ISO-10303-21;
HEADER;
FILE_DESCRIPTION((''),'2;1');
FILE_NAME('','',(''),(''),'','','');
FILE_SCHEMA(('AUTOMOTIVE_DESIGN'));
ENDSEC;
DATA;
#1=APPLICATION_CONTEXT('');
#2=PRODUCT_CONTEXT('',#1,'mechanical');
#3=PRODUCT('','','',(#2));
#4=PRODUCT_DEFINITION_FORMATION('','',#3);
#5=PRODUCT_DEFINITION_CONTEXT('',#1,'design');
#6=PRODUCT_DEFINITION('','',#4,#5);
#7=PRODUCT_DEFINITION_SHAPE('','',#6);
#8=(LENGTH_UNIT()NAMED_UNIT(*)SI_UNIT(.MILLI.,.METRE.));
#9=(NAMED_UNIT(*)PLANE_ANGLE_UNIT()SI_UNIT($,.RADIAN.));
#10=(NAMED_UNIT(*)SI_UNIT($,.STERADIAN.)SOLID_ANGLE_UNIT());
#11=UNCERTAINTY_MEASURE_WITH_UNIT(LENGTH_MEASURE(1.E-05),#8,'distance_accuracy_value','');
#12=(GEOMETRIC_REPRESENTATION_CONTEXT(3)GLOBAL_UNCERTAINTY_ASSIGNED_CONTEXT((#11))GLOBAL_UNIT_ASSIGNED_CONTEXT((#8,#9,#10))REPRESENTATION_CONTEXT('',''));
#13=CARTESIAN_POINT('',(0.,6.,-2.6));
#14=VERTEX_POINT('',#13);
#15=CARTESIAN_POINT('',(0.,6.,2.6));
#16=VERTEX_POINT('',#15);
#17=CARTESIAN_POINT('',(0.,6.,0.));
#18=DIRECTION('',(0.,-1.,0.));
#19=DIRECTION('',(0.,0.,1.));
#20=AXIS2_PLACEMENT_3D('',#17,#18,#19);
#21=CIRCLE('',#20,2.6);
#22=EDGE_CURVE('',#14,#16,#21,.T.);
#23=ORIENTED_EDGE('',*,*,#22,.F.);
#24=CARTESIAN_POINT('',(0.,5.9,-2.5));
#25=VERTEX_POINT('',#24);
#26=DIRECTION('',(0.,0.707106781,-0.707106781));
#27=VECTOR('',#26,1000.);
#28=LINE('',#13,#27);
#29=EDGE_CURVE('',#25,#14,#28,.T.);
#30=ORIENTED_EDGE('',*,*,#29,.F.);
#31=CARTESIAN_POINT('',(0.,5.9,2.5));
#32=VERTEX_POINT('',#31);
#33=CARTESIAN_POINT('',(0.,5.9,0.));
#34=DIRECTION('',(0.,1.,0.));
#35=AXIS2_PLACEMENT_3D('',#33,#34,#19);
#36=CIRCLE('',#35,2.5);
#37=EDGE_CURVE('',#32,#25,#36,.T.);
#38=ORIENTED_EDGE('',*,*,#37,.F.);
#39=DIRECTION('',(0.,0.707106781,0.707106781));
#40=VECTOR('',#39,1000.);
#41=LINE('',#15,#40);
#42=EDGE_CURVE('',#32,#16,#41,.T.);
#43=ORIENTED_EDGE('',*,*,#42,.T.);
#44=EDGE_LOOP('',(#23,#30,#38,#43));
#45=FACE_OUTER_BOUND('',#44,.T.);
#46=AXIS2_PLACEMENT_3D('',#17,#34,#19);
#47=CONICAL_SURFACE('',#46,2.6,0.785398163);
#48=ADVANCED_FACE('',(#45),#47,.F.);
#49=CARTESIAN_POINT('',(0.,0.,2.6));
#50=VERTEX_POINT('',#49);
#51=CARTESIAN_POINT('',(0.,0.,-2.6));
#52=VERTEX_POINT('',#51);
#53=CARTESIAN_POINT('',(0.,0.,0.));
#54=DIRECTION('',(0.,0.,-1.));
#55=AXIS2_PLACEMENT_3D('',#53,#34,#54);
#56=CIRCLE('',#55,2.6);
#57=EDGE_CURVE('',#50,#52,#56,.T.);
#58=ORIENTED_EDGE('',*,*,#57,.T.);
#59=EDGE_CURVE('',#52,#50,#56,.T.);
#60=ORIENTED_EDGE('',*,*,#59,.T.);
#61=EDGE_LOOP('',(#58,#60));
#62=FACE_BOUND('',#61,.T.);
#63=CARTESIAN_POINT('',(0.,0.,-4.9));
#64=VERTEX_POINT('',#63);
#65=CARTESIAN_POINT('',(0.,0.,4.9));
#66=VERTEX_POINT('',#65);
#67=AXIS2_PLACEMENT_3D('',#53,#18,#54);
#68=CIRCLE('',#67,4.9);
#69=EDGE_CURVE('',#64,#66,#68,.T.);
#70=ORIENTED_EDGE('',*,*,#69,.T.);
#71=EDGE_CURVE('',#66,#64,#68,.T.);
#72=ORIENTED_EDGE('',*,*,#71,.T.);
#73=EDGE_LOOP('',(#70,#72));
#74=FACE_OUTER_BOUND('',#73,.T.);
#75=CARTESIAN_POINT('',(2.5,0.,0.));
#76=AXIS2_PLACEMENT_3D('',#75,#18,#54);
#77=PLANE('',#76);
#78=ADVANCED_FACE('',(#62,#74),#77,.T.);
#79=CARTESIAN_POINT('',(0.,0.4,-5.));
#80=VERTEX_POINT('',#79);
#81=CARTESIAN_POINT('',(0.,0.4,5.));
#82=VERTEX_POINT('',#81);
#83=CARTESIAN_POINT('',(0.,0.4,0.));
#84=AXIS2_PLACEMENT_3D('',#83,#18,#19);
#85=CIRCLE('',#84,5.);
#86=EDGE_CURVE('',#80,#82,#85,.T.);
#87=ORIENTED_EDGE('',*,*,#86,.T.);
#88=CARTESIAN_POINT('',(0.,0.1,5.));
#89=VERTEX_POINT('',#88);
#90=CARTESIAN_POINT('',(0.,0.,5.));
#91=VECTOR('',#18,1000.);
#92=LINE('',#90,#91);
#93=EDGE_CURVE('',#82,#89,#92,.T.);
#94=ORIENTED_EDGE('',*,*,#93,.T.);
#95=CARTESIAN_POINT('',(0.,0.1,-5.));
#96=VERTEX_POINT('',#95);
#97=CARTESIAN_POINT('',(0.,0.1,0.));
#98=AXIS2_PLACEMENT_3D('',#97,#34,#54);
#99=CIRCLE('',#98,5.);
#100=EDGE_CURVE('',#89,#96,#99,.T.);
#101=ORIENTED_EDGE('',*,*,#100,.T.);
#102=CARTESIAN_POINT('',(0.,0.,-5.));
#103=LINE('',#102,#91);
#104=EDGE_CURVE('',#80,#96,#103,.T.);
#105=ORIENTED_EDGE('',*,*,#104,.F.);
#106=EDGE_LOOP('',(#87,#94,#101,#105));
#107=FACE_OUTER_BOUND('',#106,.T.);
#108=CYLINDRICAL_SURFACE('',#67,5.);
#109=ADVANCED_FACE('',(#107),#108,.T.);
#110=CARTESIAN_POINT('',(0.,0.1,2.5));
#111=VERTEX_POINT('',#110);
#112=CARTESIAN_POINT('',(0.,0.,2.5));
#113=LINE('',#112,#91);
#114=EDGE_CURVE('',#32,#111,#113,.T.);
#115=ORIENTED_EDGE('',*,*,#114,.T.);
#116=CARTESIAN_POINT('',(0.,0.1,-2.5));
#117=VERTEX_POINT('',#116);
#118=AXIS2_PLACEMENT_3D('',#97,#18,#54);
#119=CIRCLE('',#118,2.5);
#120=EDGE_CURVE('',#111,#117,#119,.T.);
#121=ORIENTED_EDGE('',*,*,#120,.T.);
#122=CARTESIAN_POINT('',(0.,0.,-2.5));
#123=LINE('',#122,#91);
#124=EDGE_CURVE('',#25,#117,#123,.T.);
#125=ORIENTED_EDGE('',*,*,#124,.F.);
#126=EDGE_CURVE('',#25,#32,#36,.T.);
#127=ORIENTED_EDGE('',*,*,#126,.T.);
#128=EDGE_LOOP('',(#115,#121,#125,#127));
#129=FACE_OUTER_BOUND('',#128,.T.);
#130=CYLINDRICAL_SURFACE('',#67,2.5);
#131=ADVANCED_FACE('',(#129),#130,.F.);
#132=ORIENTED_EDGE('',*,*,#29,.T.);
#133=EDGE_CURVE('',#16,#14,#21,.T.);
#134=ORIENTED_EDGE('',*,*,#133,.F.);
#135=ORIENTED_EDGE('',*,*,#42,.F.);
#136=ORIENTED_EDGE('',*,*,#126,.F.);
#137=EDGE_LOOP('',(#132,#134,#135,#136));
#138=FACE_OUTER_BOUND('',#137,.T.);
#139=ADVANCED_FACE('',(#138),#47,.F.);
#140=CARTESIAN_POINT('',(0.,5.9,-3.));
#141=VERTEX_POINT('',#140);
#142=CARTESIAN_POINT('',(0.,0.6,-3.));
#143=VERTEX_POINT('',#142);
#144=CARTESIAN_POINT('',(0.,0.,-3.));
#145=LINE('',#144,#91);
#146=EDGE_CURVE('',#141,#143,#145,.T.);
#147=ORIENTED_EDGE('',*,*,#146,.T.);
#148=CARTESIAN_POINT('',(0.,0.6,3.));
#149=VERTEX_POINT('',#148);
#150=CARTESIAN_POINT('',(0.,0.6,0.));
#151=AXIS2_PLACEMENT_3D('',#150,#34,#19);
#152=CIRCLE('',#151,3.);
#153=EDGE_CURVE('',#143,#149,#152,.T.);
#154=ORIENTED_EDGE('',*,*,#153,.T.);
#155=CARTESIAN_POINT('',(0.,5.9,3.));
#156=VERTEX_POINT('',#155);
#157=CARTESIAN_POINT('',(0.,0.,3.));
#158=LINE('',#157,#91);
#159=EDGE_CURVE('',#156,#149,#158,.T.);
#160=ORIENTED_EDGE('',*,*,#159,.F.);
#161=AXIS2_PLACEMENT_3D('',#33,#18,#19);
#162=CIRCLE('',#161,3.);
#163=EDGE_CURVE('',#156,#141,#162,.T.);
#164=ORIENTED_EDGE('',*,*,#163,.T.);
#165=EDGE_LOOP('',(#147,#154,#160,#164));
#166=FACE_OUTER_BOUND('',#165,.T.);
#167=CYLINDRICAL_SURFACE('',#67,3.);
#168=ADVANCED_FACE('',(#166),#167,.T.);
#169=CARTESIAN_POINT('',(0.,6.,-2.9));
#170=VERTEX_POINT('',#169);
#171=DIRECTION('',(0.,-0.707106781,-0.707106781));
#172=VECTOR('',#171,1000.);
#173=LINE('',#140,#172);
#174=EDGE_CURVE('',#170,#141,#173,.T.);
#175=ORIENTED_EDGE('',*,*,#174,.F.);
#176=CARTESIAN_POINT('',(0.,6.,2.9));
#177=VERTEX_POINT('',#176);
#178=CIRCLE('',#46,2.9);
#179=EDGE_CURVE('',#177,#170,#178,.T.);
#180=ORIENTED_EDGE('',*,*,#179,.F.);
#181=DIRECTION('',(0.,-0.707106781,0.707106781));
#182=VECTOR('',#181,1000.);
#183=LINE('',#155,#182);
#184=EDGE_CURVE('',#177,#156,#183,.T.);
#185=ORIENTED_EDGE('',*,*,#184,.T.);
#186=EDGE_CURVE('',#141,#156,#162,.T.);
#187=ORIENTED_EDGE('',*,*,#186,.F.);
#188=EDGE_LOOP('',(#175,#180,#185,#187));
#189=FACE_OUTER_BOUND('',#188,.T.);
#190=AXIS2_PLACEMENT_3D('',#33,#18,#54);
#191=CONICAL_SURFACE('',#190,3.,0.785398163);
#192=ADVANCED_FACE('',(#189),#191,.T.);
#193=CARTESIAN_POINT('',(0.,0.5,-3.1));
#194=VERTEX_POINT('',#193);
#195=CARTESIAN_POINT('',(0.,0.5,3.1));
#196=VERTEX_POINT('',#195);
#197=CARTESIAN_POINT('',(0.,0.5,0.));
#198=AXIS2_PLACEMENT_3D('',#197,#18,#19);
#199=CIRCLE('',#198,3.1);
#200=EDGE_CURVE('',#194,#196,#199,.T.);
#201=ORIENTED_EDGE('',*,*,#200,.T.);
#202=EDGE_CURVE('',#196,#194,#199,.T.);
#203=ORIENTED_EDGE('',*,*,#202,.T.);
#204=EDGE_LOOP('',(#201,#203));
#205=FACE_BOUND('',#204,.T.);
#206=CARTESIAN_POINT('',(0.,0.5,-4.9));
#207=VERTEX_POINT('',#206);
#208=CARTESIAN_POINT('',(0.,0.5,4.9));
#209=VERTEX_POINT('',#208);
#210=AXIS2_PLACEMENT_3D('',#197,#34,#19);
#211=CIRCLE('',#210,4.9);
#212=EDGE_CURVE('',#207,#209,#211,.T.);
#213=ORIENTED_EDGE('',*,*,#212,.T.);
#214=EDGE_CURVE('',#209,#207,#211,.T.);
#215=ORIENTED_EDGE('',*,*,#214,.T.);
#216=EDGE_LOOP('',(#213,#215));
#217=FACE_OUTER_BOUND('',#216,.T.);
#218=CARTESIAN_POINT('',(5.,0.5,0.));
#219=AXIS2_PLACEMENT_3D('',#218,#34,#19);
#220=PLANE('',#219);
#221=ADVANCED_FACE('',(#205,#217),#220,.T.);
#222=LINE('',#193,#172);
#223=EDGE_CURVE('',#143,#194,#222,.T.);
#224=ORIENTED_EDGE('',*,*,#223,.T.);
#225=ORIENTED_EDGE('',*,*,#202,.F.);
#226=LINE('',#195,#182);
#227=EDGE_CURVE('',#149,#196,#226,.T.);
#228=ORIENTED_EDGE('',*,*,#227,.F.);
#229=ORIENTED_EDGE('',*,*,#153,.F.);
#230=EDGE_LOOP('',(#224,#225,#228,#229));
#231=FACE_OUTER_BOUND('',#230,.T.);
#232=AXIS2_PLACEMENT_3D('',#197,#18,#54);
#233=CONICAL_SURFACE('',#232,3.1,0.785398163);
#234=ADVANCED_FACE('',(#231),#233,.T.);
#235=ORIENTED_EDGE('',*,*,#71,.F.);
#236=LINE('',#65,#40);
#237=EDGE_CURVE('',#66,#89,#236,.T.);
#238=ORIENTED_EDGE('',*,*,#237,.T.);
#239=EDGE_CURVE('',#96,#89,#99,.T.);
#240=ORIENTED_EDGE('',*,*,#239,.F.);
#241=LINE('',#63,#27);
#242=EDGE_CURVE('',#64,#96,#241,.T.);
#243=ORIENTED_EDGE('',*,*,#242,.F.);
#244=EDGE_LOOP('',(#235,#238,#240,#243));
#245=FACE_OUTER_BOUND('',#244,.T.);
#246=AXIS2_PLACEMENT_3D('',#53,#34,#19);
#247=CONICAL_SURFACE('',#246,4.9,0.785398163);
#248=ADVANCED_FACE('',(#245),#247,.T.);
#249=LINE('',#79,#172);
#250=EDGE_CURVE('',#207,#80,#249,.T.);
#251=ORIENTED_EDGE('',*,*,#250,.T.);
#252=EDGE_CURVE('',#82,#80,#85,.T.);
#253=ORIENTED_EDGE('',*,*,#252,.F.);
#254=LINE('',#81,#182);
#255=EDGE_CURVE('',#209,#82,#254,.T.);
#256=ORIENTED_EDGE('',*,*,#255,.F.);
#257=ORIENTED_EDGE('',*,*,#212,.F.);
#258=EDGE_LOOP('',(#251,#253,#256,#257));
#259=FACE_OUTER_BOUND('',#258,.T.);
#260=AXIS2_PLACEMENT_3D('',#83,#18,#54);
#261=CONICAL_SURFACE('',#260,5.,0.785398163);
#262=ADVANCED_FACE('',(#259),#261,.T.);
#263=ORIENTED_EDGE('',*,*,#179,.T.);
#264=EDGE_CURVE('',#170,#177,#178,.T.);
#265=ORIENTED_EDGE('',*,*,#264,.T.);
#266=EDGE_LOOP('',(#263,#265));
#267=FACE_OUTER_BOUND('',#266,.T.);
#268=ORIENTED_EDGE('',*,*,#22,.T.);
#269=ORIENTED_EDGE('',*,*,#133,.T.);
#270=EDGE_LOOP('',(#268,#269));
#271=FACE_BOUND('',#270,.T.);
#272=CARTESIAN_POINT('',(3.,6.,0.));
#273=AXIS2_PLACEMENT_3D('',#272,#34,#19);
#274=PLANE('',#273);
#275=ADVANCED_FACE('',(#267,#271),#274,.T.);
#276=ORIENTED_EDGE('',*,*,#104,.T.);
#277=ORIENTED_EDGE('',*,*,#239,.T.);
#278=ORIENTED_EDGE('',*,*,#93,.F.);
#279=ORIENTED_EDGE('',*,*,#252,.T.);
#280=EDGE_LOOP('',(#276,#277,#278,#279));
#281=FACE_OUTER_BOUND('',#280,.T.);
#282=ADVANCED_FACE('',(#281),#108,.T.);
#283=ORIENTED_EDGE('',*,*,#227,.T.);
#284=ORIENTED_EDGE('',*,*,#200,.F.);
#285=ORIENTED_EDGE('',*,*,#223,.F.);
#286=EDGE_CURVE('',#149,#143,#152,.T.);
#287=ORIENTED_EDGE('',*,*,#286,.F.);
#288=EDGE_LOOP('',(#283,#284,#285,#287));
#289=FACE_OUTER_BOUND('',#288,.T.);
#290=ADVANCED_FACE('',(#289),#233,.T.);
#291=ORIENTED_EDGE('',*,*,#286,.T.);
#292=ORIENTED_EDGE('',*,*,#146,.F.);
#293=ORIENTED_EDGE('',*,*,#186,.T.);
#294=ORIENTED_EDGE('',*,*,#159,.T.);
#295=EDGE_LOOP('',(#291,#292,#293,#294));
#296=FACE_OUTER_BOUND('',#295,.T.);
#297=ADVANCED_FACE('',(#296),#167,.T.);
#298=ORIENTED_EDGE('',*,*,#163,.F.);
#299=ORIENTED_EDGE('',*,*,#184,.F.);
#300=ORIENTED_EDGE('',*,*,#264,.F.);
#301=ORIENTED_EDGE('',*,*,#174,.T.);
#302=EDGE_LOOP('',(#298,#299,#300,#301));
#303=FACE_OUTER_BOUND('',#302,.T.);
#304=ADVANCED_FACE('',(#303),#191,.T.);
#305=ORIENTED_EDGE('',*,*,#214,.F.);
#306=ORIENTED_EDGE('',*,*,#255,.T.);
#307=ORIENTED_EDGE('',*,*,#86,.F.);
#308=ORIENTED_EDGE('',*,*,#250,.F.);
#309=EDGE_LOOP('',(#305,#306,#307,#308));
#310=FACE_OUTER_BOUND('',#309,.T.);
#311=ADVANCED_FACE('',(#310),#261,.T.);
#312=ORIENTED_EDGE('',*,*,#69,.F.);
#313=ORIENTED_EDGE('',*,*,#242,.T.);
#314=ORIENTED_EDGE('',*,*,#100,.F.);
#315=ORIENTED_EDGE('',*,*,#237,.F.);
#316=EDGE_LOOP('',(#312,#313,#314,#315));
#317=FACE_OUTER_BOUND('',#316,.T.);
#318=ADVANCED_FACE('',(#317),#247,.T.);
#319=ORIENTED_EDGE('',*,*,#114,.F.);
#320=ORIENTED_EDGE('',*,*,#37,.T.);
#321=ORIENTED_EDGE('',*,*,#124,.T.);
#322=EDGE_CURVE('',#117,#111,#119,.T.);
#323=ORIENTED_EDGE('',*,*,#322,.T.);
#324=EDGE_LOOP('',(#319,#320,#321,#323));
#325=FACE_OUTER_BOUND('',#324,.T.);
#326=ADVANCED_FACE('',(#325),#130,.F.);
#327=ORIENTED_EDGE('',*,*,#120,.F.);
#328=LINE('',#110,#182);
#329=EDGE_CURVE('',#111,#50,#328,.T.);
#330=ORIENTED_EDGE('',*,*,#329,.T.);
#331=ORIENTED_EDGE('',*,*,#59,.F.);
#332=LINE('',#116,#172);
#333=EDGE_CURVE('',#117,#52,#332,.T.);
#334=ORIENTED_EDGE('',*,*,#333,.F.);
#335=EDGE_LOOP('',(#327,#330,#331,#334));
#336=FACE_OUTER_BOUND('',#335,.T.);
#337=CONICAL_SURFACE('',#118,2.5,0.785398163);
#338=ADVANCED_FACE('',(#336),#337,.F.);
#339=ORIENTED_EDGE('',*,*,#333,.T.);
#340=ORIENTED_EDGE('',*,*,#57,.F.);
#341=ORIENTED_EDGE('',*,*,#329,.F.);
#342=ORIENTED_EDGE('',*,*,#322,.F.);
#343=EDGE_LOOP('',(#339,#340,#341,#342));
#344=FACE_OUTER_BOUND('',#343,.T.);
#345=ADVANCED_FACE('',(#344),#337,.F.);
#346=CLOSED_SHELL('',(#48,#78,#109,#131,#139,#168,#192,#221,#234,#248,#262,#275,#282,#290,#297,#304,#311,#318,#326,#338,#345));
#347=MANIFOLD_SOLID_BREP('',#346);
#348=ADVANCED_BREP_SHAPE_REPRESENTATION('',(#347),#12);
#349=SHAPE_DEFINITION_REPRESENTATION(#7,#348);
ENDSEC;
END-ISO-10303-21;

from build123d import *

# Parameters (mm, degrees)
CHAMFER_1_SIZE = 0.1


with BuildPart() as part:
    # 草图1 → 旋转1 (revolve)
    with BuildSketch(Plane.XY, mode=Mode.PRIVATE) as revolve_1_sk:
        Polygon((2.5, 0), (5, 0), (5, 0.5), (3, 0.5), (3, 6), (2.5, 6), align=None)
    revolve(revolve_1_sk.sketch.rotate(Axis((0, 0, 0), (0, 1, 0)), 90), axis=Axis((0, 0, 0), (0, 1, 0)))

    # 倒角1
    chamfer_1_edges = [part.edges().sort_by_distance(p)[0] for p in [
        (0, 6, 2.5),
        (0, 6, 3),
        (0, 0.5, 3),
        (0, 0.5, 5),
        (0, 0, 5),
        (0, 0, 2.5),
    ]]
    chamfer(chamfer_1_edges, length=CHAMFER_1_SIZE)


solid = part.part
